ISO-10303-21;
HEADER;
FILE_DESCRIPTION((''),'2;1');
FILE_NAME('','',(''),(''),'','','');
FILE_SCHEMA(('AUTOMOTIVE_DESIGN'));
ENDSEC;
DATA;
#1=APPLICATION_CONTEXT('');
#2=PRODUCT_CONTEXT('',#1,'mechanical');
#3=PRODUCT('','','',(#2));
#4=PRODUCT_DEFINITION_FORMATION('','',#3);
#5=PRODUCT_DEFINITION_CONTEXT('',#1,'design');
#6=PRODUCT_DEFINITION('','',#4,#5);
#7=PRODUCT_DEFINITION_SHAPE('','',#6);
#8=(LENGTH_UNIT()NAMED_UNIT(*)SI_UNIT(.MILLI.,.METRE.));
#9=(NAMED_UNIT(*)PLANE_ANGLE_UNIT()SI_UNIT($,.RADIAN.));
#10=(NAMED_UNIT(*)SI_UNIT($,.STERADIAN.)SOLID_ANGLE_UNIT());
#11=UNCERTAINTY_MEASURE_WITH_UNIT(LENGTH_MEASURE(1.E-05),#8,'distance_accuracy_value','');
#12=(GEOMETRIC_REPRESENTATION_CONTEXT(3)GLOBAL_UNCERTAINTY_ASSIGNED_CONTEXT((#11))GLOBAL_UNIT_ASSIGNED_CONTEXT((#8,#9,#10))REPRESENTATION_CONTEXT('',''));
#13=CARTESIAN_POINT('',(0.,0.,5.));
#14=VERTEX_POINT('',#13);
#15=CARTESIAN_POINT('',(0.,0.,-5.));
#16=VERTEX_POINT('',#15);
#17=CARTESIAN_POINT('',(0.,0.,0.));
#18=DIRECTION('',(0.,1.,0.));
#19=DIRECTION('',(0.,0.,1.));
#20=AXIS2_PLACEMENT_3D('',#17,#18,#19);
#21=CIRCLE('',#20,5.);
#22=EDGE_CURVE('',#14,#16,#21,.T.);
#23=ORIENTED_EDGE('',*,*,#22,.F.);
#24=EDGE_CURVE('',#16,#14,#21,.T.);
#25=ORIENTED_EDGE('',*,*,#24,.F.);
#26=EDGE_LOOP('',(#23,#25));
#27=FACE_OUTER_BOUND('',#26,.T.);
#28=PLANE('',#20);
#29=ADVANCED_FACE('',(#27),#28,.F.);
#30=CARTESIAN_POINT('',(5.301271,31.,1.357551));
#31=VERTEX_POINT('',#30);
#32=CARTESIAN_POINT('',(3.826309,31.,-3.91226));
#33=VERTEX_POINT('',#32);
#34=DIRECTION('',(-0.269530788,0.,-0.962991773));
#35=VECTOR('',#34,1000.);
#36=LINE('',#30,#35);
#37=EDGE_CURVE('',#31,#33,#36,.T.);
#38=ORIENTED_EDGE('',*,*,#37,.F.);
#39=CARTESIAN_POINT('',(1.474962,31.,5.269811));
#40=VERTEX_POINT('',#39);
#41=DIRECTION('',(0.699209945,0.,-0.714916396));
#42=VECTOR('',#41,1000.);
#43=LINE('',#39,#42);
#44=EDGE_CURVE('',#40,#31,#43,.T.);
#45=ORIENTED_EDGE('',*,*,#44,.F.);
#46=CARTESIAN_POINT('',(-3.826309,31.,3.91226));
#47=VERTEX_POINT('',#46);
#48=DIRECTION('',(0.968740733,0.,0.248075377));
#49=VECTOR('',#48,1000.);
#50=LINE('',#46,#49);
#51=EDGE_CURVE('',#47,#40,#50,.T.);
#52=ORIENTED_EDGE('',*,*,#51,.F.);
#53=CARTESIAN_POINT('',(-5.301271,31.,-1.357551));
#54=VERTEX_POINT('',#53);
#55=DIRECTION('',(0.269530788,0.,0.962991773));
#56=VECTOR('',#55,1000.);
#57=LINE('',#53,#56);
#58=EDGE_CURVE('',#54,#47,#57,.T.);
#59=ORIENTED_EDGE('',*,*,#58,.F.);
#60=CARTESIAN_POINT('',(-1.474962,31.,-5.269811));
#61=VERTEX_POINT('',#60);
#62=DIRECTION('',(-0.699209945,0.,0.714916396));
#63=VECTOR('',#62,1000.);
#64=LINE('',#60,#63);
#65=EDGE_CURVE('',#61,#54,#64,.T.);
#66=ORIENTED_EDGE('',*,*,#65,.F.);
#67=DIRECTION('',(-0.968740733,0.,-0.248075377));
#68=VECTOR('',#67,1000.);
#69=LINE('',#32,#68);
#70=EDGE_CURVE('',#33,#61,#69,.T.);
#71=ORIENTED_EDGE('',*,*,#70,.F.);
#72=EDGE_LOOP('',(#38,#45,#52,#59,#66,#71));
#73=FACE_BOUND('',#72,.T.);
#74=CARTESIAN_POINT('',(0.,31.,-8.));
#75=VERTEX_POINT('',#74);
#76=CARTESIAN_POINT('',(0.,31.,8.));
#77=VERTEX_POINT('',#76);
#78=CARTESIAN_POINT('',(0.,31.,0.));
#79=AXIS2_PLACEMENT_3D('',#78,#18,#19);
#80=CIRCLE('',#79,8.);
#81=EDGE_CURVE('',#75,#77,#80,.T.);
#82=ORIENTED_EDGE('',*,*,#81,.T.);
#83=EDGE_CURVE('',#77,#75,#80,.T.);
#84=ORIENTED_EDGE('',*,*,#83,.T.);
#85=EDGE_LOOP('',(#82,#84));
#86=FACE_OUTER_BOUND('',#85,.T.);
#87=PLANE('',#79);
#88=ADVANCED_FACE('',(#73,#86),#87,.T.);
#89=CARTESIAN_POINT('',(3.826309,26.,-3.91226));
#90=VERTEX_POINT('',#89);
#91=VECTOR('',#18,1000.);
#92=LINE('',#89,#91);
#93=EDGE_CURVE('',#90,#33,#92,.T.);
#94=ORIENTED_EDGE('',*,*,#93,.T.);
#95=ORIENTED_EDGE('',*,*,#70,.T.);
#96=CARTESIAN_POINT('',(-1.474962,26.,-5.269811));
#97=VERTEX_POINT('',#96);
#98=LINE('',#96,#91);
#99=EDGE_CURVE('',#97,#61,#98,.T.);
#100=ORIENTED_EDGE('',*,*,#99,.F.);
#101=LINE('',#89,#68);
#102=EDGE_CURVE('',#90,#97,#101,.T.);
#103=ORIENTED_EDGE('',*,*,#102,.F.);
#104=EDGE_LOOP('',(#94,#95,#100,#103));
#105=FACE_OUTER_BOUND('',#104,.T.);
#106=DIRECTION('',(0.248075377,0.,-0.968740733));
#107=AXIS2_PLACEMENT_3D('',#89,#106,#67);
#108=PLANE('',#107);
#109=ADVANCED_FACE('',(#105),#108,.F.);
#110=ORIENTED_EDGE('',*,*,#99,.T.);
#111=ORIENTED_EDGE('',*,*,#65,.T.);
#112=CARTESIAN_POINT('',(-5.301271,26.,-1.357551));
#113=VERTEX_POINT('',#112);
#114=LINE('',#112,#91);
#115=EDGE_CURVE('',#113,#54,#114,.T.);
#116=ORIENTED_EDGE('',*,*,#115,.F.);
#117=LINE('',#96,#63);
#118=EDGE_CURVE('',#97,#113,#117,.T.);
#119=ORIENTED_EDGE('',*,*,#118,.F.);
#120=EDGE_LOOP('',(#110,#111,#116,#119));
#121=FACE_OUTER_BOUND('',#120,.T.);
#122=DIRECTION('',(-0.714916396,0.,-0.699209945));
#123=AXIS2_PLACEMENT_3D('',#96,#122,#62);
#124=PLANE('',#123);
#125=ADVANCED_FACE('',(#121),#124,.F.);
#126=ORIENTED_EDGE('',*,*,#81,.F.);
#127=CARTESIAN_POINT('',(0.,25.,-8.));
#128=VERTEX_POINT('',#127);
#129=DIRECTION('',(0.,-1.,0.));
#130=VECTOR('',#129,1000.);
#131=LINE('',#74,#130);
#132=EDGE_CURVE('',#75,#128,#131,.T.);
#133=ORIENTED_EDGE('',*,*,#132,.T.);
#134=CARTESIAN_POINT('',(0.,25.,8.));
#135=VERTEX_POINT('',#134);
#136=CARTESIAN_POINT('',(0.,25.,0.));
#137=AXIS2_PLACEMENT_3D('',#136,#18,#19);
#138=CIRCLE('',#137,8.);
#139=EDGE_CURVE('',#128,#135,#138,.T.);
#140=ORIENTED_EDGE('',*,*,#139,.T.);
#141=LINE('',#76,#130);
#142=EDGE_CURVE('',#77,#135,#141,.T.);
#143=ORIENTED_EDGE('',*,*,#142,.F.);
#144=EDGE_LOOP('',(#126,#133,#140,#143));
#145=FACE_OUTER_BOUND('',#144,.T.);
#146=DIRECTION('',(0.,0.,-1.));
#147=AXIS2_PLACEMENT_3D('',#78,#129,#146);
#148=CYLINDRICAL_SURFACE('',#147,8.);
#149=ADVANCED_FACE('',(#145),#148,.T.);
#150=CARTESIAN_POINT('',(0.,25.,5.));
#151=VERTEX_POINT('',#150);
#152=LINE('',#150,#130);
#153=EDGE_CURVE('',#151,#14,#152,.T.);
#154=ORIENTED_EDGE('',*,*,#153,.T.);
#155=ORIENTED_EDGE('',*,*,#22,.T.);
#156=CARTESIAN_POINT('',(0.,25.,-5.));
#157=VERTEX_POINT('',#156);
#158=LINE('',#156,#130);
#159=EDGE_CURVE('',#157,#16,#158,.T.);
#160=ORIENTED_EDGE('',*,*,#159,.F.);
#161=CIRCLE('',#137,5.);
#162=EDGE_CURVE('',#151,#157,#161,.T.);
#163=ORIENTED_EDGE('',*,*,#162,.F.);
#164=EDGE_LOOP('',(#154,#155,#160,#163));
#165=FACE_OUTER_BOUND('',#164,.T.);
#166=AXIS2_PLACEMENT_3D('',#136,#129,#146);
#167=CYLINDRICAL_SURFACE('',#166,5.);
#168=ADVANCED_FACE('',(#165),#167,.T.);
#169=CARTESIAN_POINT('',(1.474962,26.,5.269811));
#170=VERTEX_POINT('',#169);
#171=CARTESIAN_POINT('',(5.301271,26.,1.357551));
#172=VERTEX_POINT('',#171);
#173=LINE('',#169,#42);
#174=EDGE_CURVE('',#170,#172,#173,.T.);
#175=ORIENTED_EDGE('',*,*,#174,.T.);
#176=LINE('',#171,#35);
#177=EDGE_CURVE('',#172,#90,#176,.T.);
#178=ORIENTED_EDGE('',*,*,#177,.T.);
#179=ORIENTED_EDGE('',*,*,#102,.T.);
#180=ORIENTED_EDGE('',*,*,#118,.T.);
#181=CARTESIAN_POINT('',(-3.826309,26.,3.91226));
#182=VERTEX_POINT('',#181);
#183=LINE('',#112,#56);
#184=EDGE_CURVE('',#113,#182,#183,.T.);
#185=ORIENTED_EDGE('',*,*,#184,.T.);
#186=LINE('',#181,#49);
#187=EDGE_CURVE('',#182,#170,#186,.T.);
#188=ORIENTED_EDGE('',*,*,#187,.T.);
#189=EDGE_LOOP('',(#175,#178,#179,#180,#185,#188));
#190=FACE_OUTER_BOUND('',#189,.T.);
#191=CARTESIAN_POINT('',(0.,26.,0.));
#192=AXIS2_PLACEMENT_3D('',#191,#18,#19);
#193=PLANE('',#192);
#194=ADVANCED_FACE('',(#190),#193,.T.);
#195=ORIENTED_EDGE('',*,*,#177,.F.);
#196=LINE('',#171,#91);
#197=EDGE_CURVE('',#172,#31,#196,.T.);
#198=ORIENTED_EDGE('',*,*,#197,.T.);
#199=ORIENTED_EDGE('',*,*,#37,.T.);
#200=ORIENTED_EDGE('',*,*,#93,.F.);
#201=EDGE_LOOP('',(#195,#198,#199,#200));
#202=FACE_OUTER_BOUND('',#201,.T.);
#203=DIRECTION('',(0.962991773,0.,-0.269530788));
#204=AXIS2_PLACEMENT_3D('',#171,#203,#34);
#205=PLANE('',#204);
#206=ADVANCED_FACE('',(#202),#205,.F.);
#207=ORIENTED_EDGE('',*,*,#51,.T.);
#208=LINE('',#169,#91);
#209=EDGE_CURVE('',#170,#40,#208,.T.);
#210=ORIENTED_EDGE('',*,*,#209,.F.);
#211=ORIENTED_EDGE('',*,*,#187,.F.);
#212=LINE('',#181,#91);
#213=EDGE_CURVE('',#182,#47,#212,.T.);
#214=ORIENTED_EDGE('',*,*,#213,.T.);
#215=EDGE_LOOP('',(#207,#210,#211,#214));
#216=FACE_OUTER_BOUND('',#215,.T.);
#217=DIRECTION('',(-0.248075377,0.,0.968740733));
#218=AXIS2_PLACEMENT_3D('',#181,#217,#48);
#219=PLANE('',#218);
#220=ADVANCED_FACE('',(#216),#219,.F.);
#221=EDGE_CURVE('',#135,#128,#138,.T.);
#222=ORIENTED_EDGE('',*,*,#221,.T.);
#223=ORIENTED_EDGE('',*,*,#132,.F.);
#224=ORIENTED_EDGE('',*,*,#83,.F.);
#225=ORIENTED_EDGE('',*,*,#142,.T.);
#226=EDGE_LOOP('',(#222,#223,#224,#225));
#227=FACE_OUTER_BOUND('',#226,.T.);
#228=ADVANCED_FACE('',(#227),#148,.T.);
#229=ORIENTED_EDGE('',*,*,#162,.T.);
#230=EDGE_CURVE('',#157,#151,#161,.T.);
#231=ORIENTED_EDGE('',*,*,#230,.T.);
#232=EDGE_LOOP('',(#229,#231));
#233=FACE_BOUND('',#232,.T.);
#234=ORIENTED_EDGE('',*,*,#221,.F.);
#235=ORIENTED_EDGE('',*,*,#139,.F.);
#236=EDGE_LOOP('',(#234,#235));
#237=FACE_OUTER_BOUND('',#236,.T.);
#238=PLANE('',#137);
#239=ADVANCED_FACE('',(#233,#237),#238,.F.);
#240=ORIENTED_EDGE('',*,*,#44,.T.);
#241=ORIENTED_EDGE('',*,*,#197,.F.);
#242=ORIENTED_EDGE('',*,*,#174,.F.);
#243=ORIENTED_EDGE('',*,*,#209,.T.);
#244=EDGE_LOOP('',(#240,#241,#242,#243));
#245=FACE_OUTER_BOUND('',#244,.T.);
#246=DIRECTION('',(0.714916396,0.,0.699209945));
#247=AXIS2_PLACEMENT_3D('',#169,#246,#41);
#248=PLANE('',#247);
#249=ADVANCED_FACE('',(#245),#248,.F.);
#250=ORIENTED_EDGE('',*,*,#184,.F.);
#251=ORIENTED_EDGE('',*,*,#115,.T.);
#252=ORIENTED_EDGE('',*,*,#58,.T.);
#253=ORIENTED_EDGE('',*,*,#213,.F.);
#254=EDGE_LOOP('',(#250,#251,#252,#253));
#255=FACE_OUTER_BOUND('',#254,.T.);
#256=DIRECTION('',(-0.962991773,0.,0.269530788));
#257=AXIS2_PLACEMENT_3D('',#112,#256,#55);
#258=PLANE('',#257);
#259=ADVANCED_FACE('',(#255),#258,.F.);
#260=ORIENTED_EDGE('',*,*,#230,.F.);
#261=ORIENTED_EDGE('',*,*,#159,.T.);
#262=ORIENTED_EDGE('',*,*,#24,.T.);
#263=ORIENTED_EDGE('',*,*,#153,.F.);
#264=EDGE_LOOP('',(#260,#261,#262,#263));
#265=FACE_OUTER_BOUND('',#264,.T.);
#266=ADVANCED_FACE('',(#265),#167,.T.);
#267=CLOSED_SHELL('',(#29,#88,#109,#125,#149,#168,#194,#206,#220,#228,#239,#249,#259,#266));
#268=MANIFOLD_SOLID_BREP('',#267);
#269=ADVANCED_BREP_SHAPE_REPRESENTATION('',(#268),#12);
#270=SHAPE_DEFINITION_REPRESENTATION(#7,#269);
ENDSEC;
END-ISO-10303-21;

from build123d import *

# Parameters (mm, degrees)
SKETCH1_R           = 5
BOSS_EXTRUDE1_DEPTH = 25
SKETCH2_R           = 8
BOSS_EXTRUDE2_DEPTH = 6
CUT_EXTRUDE1_DEPTH  = 5


with BuildPart() as part:
    # Sketch1 → Boss-Extrude1 (new body)
    with BuildSketch(Plane(origin=(0, 0, 0), x_dir=(1, 0, 0), z_dir=(0, 1, 0))):
        with Locations(Location((0, 0, 0), (0, 0, 270))):
            Circle(SKETCH1_R)
    extrude(amount=BOSS_EXTRUDE1_DEPTH)

    # Sketch2 → Boss-Extrude2 (add)
    with BuildSketch(Plane(origin=(0, 25, 0), x_dir=(1, 0, 0), z_dir=(0, 1, 0))):
        with Locations(Location((0, 0, 0), (0, 0, 270))):
            Circle(SKETCH2_R)
    extrude(amount=BOSS_EXTRUDE2_DEPTH)

    # Sketch3 → Cut-Extrude1 (cut)
    with BuildSketch(Plane(origin=(0, 31, 0), x_dir=(1, 0, 0), z_dir=(0, 1, 0))):
        Polygon((-1.474961989, 5.269810816), (-5.301271034, 1.357550856), (-3.826309045, -3.91225996), (1.474961989, -5.269810816), (5.301271034, -1.357550856), (3.826309045, 3.91225996), align=None)
    extrude(amount=-CUT_EXTRUDE1_DEPTH, mode=Mode.SUBTRACT)


solid = part.part
